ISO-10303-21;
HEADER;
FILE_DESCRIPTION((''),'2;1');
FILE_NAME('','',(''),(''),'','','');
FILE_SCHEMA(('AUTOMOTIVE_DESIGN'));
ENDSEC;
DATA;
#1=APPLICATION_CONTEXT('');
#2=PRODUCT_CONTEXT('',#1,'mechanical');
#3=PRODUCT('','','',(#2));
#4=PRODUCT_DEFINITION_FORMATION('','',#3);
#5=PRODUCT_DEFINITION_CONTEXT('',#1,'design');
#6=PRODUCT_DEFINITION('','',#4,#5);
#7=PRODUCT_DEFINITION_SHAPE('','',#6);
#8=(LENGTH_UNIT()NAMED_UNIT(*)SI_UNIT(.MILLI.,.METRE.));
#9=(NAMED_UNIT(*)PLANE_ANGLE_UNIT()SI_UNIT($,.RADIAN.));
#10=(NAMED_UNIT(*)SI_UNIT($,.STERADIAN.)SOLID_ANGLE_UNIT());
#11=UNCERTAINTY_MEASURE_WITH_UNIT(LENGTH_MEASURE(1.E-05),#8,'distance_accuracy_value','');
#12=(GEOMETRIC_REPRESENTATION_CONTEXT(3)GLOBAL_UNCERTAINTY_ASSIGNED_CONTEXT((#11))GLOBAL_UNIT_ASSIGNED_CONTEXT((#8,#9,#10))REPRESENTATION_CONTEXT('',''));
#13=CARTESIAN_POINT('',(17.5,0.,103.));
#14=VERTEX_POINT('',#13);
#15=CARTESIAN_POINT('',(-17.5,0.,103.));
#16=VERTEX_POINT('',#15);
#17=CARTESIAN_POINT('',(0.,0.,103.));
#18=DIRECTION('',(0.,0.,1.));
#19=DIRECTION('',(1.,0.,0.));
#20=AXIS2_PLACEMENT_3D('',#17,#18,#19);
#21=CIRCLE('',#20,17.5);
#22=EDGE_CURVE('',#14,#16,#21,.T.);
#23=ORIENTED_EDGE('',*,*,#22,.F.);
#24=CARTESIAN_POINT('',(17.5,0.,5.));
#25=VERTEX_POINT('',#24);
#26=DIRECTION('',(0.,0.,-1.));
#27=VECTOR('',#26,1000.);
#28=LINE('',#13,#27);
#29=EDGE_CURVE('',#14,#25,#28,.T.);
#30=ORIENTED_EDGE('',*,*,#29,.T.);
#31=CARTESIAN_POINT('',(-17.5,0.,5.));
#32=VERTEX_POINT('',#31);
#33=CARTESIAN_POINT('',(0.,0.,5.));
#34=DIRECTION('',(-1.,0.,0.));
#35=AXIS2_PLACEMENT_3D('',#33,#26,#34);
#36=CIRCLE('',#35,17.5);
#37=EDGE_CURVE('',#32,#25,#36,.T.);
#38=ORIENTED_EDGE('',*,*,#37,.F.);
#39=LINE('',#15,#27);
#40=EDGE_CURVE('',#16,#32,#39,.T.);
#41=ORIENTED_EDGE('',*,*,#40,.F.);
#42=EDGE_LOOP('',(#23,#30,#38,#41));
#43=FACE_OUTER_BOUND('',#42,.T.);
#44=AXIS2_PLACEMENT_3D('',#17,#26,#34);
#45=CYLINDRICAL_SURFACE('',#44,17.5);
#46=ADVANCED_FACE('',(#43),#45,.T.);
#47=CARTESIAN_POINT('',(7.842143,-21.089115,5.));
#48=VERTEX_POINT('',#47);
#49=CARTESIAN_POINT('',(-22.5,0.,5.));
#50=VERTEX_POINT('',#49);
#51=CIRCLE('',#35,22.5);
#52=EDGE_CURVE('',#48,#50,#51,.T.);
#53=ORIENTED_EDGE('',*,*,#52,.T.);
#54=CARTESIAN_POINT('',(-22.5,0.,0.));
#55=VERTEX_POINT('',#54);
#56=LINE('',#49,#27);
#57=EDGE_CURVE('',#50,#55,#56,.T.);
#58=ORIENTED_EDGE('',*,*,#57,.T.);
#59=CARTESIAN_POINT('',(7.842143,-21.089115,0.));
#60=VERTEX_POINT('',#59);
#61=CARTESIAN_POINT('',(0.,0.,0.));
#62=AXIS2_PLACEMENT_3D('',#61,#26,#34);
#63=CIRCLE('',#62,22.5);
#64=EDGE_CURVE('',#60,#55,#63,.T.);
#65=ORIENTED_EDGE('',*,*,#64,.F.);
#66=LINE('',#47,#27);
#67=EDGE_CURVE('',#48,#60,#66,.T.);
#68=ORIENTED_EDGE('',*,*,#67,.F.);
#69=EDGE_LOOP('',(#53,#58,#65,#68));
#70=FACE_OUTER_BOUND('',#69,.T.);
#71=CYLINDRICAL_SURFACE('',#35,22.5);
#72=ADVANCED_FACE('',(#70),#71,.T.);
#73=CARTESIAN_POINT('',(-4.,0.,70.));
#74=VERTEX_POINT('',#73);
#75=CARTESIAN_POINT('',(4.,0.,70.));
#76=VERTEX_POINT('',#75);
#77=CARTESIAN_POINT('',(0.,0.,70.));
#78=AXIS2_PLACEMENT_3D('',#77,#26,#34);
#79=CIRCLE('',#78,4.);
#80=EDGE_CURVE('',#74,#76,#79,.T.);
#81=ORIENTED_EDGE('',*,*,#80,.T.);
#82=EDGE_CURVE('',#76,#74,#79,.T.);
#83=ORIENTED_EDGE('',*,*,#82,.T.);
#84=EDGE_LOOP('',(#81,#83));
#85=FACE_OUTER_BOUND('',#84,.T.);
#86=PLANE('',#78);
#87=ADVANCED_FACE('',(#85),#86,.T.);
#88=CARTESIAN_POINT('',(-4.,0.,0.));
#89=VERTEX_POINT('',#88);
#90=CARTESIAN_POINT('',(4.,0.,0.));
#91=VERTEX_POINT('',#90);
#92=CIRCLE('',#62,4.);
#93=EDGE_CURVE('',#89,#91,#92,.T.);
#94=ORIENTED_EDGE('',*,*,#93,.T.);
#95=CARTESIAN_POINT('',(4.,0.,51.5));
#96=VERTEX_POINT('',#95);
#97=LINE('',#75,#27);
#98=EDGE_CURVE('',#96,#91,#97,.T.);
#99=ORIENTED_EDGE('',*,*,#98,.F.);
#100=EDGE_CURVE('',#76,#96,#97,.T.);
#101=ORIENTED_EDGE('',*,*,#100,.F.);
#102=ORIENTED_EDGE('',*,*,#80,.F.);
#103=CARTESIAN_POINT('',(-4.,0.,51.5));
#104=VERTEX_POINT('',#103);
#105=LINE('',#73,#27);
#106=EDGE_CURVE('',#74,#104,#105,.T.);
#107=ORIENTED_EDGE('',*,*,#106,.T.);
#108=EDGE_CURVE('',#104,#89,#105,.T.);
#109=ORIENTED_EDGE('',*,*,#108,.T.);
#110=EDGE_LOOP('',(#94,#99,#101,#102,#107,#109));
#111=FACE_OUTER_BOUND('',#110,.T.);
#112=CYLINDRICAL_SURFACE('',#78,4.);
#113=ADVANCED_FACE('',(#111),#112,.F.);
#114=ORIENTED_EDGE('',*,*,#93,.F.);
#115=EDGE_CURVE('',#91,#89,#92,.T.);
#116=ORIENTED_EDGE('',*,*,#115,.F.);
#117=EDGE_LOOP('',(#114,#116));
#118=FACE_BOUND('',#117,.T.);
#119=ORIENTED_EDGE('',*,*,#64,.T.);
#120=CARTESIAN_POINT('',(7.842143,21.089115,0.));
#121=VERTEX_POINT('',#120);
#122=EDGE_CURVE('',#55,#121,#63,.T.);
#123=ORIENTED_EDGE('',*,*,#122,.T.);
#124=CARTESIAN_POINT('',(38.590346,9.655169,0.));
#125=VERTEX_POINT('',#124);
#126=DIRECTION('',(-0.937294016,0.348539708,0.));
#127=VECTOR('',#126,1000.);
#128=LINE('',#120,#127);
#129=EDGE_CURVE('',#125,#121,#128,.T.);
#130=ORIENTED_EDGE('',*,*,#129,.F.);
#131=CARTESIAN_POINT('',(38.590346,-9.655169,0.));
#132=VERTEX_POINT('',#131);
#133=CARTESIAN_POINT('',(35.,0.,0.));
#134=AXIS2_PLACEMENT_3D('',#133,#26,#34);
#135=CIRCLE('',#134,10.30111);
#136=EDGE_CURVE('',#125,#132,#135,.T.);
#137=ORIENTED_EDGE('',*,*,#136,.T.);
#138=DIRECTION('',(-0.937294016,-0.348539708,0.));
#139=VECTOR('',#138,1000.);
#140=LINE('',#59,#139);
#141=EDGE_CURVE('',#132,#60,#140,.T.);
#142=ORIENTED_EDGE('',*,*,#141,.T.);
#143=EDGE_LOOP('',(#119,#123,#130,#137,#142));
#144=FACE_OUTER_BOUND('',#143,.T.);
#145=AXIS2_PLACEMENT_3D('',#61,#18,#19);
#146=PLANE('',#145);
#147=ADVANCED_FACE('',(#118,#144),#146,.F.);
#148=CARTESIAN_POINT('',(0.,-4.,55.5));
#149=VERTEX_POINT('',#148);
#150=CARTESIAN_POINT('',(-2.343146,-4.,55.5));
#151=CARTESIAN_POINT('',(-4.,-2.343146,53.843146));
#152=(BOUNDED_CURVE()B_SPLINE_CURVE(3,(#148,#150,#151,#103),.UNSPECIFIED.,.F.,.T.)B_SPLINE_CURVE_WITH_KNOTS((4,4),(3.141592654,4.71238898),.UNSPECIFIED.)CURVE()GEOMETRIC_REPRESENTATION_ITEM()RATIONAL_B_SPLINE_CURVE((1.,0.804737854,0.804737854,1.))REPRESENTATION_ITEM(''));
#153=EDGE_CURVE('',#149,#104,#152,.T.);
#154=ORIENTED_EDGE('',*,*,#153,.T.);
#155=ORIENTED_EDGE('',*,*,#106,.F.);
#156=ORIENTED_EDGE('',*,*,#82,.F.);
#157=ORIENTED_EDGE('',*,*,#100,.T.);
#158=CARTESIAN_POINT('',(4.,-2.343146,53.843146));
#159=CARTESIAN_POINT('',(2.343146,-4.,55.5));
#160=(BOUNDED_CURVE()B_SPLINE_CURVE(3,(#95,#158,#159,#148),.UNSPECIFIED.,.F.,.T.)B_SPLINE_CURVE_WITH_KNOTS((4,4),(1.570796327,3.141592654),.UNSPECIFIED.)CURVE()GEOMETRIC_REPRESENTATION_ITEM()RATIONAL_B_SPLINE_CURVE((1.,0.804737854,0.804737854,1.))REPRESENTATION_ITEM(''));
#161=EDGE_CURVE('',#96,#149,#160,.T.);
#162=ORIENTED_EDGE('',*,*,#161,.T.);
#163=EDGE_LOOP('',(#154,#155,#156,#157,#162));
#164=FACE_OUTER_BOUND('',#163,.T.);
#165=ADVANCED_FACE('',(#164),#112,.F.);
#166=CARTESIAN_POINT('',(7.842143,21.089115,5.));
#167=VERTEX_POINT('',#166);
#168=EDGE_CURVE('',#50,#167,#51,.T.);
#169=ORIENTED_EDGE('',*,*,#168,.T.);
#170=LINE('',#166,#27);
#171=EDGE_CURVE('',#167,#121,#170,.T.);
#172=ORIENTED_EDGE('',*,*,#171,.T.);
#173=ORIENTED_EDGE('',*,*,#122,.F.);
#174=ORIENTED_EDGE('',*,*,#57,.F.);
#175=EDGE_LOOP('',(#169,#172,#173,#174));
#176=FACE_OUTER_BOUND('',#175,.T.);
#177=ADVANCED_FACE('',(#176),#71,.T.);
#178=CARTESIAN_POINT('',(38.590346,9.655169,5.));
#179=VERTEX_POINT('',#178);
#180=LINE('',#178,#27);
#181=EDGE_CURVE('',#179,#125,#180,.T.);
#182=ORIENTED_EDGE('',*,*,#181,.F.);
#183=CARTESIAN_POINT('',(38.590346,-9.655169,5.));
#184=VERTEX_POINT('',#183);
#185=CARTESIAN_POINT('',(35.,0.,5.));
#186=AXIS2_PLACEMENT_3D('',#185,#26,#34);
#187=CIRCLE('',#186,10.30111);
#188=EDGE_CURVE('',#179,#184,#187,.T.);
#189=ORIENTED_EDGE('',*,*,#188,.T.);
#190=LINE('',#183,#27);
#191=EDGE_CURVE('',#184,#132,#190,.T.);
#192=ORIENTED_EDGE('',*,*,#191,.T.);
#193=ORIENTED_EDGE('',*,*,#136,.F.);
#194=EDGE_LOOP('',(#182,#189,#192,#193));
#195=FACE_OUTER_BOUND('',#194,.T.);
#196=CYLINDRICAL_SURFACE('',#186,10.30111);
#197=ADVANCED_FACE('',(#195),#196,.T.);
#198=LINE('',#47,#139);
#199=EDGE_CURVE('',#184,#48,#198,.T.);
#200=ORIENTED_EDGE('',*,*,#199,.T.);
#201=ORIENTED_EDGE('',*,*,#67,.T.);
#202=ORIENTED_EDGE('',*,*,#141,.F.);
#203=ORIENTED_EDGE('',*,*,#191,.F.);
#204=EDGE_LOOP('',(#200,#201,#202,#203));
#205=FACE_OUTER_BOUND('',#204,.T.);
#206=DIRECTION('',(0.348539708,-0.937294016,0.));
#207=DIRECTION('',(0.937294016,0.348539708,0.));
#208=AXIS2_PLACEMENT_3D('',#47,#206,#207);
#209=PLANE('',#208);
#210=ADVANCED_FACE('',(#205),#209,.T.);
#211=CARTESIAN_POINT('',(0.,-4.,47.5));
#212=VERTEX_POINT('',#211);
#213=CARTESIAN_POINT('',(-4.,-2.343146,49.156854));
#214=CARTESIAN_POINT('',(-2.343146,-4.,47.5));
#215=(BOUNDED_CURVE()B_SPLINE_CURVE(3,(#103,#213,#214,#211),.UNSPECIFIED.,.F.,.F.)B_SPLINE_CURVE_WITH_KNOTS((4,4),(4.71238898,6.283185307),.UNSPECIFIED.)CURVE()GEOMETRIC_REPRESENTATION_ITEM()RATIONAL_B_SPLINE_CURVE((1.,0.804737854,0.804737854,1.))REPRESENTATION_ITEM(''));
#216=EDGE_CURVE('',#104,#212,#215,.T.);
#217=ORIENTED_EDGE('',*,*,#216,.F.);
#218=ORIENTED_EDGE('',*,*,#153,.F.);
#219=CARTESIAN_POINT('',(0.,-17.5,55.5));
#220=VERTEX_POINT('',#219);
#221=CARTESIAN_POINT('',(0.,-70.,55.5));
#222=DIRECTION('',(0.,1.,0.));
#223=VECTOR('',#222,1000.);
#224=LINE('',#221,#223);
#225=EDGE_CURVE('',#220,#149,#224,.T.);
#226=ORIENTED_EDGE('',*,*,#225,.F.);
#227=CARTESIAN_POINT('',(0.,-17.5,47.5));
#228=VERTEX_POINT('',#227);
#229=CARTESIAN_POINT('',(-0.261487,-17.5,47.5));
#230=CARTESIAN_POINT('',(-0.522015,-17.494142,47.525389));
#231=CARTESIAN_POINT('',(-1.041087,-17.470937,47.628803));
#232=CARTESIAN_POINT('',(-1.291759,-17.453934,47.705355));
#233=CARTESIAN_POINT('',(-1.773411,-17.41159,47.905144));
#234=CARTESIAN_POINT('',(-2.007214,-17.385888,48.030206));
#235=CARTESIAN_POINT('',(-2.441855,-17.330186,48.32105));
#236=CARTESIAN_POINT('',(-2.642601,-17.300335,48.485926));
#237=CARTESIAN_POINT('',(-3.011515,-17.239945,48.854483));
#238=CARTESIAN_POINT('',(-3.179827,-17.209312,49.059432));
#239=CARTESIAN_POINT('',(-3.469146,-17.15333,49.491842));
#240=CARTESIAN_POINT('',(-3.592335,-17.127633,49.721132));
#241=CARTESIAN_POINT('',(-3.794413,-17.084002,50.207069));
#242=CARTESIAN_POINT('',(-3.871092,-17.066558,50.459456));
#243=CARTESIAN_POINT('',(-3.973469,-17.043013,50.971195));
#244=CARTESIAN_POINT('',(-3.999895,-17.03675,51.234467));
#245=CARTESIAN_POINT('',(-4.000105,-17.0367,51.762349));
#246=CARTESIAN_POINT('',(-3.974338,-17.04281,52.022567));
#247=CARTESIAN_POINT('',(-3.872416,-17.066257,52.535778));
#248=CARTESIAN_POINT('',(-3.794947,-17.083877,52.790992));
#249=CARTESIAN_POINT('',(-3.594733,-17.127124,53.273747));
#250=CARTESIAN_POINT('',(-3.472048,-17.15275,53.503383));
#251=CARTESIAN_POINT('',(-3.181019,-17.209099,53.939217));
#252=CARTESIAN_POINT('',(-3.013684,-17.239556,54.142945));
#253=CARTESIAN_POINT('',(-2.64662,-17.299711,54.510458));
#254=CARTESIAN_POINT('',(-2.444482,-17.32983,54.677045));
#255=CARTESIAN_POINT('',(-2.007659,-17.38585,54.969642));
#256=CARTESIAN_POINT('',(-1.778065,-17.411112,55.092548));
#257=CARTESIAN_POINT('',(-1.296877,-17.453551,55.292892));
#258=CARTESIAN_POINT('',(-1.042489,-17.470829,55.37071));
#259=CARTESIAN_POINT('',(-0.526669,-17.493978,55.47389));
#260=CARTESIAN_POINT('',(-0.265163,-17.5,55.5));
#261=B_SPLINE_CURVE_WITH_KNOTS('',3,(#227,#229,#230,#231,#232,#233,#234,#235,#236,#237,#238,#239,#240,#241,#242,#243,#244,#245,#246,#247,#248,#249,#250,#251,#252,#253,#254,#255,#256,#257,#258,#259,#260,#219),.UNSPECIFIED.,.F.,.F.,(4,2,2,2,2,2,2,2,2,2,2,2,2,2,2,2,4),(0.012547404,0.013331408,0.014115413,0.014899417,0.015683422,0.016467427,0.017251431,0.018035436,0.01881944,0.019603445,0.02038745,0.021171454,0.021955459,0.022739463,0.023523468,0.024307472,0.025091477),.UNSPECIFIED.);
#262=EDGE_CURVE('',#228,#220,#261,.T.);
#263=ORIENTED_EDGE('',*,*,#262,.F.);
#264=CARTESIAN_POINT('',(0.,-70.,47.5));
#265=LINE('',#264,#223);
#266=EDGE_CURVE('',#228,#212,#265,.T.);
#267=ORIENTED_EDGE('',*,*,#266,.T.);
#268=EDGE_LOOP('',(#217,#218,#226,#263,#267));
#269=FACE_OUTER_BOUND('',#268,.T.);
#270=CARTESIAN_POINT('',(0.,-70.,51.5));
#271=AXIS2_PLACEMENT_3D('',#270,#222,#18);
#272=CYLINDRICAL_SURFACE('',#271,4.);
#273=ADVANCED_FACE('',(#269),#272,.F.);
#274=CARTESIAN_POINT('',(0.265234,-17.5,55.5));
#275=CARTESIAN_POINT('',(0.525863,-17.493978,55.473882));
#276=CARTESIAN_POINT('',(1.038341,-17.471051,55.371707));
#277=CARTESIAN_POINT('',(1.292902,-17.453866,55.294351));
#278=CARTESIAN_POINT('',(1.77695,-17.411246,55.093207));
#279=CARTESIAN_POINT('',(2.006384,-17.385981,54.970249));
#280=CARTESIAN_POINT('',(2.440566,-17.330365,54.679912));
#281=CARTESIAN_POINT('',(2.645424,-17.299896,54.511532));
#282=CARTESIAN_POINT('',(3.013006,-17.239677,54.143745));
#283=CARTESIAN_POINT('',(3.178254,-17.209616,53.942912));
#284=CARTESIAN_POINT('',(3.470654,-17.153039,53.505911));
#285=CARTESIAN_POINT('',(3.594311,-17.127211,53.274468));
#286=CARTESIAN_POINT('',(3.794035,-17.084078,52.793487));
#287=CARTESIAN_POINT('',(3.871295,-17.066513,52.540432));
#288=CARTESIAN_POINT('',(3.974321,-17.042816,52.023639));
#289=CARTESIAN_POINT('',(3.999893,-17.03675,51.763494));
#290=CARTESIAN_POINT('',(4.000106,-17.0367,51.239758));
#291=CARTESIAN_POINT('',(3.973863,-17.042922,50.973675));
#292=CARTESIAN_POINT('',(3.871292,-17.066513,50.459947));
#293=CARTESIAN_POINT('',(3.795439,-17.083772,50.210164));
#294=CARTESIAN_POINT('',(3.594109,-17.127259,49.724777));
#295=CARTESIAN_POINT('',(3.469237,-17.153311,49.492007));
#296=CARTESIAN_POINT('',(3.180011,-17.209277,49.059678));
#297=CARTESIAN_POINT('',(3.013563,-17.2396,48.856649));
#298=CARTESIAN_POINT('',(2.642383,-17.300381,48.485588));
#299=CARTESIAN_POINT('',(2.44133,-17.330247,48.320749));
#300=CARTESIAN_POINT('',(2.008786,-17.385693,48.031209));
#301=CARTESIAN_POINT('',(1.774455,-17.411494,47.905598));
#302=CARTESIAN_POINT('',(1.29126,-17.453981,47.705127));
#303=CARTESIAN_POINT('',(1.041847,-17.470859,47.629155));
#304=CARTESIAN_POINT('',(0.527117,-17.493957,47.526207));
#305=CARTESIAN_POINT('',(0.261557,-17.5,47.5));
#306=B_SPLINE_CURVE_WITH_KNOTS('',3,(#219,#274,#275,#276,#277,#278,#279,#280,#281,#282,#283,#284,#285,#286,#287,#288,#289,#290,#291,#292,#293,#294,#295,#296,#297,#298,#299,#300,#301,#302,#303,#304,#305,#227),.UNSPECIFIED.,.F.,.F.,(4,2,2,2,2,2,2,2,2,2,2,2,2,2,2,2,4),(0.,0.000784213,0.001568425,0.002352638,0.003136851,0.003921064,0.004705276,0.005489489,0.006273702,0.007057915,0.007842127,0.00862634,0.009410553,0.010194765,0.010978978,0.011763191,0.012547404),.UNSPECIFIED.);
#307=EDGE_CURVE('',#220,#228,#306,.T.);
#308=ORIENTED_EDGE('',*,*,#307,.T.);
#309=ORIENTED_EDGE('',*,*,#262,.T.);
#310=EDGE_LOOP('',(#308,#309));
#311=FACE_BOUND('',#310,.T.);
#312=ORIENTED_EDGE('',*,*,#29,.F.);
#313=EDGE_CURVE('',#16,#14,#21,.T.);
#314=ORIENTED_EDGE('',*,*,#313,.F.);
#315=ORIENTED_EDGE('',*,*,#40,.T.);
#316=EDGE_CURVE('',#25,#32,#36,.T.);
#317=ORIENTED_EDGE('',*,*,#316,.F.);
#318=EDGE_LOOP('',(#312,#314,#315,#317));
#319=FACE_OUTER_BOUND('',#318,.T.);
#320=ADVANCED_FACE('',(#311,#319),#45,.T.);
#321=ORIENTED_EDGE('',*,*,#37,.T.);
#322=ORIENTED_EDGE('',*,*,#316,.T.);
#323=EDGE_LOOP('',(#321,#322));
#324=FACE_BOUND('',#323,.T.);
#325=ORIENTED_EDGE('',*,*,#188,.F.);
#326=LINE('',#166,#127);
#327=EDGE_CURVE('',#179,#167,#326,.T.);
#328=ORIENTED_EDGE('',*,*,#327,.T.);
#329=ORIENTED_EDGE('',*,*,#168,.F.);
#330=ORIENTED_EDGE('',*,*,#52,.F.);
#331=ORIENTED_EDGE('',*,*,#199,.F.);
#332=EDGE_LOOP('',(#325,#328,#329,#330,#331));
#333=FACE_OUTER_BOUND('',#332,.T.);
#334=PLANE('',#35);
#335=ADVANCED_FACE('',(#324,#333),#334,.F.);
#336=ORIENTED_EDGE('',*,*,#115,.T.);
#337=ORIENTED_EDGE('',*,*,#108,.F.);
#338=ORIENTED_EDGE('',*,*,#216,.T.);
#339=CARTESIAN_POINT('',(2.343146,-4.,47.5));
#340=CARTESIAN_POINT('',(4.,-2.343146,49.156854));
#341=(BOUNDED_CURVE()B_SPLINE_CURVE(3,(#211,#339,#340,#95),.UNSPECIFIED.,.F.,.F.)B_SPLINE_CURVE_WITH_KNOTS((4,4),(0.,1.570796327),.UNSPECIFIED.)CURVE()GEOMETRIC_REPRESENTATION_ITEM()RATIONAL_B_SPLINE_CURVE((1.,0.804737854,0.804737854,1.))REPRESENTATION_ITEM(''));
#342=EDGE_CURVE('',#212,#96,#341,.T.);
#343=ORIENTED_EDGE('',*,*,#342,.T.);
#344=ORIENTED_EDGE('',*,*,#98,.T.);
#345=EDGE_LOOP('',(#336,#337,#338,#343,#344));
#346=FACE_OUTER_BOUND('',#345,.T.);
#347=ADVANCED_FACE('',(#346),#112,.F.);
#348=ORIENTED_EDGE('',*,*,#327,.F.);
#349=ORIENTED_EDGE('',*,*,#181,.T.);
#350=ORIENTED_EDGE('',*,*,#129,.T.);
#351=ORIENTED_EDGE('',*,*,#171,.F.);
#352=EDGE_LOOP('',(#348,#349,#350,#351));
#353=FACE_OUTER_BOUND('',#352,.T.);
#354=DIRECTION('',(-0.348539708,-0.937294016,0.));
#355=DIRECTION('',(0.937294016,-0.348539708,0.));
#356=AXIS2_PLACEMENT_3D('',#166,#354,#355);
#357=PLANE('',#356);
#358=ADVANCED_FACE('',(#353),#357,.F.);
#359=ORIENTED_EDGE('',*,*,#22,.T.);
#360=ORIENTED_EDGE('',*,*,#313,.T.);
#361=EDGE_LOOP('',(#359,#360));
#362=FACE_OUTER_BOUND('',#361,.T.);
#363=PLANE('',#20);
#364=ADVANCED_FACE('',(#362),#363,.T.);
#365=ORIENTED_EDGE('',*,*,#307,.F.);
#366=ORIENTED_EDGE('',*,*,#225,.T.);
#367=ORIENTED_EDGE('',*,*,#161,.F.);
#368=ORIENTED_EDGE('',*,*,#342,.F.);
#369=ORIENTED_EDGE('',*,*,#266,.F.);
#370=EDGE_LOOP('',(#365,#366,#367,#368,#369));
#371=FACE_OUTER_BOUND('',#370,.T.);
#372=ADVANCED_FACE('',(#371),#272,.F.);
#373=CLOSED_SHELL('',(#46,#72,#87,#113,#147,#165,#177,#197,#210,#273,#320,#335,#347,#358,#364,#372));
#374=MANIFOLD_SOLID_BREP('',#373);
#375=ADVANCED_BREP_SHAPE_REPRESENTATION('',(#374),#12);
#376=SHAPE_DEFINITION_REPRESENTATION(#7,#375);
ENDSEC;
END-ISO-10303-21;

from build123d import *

# Parameters (mm, degrees)
SKETCH_1_R          = 17.5
EXTRUDE_1_DEPTH     = 103
SKETCH_2_R          = 17.5
EXTRUDE_3_DEPTH     = 5
SKETCH_3_R          = 4
CUT_EXTRUDE_1_DEPTH = 70
CUT_EXTRUDE_2_DEPTH = 70


with BuildPart() as part:
    # 草图1 → 凸台-拉伸1 (new body)
    with BuildSketch(Plane.XY):
        Circle(SKETCH_1_R)
    extrude(amount=EXTRUDE_1_DEPTH)

    # 草图2 → 凸台-拉伸3 (add)
    with BuildSketch(Plane(origin=(0, 0, 0), x_dir=(-1, 0, 0), z_dir=(0, 0, -1))):
        with BuildLine():
            Line((-7.842143419, 21.089115358), (-38.590345949, 9.655168982))
            ThreePointArc((-38.590345949, 9.655168982), (-45.301110237, 0), (-38.590345949, -9.655168982))
            Line((-38.590345949, -9.655168982), (-7.842143419, -21.089115358))
            ThreePointArc((-7.842143419, -21.089115358), (22.5, 0), (-7.842143419, 21.089115358))
        make_face()
        Circle(SKETCH_2_R, mode=Mode.SUBTRACT)
    extrude(amount=-EXTRUDE_3_DEPTH)

    # 草图3 → 切除-拉伸1 (cut)
    with BuildSketch(Plane(origin=(0, 0, 0), x_dir=(-1, 0, 0), z_dir=(0, 0, -1))):
        Circle(SKETCH_3_R)
    extrude(amount=-CUT_EXTRUDE_1_DEPTH, mode=Mode.SUBTRACT)

    # 草图4 → 切除-拉伸2 (cut)
    with BuildSketch(Plane(origin=(0, 0, 0), x_dir=(1, 0, 0), z_dir=(0, 1, 0))):
        with BuildLine():
            Line((0, -51.5), (0, -55.5))
            ThreePointArc((0, -55.5), (2.828427125, -54.328427125), (4, -51.5))
            Line((4, -51.5), (0, -51.5))
        make_face()
        with BuildLine():
            Line((0, -47.5), (0, -51.5))
            Line((0, -51.5), (4, -51.5))
            ThreePointArc((4, -51.5), (2.828427125, -48.671572875), (0, -47.5))
        make_face()
        with BuildLine():
            ThreePointArc((0, -47.5), (-4, -51.5), (0, -55.5))
            Line((0, -55.5), (0, -51.5))
            Line((0, -51.5), (0, -47.5))
        make_face()
    extrude(amount=-CUT_EXTRUDE_2_DEPTH, mode=Mode.SUBTRACT)


solid = part.part
